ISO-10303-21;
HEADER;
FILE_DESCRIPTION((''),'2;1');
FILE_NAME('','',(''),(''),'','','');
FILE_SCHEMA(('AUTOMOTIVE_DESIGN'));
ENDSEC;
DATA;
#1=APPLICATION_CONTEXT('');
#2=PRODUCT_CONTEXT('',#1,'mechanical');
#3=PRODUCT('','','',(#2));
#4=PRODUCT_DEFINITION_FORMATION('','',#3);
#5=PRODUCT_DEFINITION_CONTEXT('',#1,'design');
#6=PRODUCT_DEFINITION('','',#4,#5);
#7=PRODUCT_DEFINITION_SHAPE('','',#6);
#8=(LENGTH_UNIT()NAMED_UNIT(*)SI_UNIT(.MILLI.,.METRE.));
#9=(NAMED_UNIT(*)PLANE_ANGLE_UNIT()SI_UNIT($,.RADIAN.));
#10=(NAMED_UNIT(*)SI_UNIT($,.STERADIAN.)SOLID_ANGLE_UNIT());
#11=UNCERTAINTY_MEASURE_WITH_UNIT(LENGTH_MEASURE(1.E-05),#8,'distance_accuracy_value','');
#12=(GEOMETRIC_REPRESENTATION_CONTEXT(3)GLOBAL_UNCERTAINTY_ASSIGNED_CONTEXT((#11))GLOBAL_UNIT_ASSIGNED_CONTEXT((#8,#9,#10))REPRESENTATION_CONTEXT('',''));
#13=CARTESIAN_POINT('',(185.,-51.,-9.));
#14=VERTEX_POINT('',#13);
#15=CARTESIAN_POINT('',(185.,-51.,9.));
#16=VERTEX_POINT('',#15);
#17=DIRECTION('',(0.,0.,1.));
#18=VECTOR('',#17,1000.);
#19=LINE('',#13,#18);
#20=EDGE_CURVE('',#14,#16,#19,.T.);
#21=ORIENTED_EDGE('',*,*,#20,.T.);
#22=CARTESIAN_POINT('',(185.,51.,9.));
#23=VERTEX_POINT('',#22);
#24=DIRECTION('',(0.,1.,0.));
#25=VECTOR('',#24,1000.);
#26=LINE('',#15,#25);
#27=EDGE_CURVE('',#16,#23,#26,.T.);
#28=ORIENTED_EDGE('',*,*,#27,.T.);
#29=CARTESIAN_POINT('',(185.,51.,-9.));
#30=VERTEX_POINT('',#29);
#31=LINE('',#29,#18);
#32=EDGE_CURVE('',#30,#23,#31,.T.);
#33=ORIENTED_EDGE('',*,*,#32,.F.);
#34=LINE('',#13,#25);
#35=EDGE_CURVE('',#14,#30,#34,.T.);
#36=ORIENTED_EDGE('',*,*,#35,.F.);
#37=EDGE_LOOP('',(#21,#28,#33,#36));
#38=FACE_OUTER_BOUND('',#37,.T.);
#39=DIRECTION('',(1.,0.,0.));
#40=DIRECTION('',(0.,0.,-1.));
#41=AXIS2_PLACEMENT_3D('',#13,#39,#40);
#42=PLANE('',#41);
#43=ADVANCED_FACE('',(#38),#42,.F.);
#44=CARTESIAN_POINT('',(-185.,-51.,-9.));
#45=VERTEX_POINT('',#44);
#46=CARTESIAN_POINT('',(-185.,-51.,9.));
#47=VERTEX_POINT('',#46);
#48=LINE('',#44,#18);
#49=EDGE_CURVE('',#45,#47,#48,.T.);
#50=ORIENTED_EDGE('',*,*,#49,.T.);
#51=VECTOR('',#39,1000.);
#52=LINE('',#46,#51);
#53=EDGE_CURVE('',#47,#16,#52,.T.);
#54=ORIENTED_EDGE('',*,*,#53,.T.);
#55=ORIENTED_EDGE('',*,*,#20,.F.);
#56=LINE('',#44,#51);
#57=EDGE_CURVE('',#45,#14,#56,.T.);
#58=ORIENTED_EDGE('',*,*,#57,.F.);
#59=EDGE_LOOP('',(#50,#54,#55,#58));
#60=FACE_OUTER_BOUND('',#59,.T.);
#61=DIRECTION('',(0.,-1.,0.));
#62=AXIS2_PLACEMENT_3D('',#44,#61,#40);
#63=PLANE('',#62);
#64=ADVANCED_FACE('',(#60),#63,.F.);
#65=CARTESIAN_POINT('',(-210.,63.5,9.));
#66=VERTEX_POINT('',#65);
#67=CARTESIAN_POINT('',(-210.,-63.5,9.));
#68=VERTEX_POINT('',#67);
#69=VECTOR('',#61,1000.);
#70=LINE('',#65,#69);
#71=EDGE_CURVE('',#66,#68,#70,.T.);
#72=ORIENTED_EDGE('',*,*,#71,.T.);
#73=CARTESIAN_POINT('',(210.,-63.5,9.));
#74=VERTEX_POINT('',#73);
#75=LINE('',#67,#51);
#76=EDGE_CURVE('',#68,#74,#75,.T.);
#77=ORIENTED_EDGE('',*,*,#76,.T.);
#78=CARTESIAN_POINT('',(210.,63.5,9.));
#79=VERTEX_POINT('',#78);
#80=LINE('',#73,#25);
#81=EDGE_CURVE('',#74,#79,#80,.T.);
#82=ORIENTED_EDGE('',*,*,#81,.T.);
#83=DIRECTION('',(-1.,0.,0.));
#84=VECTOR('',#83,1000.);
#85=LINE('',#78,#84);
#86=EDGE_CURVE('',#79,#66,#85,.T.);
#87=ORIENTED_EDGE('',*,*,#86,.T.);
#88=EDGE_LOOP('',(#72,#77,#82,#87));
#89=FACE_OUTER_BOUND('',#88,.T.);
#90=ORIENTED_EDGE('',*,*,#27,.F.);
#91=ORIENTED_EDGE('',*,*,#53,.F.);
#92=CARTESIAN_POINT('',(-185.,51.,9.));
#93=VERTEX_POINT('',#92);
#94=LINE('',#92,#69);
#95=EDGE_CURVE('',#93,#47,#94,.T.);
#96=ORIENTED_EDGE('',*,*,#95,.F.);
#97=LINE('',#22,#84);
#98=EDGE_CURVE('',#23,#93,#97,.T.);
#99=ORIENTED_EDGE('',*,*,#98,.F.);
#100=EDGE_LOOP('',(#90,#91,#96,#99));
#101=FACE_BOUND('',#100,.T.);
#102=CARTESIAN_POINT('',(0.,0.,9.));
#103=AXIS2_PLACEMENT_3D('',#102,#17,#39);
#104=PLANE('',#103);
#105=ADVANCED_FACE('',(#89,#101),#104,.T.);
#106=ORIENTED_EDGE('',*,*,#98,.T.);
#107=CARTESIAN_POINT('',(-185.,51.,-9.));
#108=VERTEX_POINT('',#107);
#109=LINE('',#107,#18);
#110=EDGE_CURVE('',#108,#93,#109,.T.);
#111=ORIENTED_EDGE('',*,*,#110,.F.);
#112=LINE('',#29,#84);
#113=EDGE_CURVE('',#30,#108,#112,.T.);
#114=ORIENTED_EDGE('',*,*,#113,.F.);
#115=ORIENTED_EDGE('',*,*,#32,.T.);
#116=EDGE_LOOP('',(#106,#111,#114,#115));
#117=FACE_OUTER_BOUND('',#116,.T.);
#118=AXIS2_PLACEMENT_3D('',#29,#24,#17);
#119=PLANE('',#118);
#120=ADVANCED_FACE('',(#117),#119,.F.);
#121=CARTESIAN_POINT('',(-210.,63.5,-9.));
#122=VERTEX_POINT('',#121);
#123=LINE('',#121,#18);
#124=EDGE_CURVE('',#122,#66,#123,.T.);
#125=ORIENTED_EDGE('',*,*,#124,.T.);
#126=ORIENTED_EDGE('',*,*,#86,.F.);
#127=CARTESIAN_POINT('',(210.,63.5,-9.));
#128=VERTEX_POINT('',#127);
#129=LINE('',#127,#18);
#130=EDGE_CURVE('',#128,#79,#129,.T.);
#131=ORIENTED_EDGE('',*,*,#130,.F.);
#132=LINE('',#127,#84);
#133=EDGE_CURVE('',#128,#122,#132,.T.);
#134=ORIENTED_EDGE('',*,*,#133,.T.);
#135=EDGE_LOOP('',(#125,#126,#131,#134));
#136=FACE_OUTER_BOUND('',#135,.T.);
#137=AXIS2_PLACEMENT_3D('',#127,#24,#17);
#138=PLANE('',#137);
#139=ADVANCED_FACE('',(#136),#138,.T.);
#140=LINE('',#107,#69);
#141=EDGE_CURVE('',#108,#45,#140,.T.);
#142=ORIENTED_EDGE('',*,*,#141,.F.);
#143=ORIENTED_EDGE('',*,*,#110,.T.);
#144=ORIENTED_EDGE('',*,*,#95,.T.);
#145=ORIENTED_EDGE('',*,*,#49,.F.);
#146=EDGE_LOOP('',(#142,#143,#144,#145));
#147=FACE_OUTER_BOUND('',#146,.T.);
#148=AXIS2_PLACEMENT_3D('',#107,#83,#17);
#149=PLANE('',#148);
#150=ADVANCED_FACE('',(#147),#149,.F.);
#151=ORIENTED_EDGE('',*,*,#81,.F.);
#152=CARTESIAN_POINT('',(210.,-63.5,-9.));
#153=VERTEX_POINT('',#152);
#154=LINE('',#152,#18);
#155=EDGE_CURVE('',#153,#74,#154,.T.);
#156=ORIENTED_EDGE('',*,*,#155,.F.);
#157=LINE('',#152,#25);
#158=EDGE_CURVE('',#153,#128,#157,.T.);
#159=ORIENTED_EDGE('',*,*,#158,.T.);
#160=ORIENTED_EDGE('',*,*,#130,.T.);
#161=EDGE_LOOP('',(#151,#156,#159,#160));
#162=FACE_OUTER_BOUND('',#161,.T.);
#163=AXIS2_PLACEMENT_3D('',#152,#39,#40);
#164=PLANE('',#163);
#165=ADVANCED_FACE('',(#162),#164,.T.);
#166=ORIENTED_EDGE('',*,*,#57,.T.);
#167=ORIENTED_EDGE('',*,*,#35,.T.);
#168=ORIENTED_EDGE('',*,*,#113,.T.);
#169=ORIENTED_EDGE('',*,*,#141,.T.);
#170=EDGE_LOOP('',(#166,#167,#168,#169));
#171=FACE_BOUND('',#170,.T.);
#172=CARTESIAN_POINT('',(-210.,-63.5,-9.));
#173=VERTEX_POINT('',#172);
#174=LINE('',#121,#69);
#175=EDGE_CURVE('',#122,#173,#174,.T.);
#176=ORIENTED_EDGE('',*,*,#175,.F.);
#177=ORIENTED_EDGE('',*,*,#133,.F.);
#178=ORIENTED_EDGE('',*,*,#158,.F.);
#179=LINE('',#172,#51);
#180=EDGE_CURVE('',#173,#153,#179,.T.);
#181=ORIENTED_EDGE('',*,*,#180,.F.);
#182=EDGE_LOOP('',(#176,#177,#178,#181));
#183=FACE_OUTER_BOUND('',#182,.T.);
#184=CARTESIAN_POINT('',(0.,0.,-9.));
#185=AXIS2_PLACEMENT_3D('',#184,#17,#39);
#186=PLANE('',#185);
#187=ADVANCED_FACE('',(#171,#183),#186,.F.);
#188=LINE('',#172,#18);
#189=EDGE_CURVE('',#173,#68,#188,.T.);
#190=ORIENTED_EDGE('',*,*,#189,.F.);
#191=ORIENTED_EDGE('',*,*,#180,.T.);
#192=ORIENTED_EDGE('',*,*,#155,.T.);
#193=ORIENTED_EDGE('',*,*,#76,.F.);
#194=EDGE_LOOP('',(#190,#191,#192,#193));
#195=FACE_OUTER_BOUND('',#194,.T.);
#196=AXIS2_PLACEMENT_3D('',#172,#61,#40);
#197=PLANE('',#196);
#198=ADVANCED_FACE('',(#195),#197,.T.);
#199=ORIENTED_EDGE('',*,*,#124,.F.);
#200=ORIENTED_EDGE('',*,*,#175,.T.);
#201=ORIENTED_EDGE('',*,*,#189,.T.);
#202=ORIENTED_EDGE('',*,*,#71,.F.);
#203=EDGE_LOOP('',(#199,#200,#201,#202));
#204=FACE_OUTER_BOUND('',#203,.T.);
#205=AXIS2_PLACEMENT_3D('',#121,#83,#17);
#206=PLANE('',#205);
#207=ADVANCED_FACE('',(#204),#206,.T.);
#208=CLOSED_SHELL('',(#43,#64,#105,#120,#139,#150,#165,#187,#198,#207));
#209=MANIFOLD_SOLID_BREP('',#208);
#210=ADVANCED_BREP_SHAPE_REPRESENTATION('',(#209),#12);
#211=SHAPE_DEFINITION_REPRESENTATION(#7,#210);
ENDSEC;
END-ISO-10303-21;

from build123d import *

# Parameters (mm, degrees)
SKETCH_1_W      = 420
SKETCH_1_H      = 127
SKETCH_1_W_2    = 370
SKETCH_1_H_2    = 102
EXTRUDE_1_DEPTH = 9


with BuildPart() as part:
    # 草图1 → 凸台-拉伸1 (new, symmetric)
    with BuildSketch(Plane.XY):
        Rectangle(SKETCH_1_W, SKETCH_1_H)
        Rectangle(SKETCH_1_W_2, SKETCH_1_H_2, mode=Mode.SUBTRACT)
    extrude(amount=EXTRUDE_1_DEPTH, both=True)


solid = part.part
